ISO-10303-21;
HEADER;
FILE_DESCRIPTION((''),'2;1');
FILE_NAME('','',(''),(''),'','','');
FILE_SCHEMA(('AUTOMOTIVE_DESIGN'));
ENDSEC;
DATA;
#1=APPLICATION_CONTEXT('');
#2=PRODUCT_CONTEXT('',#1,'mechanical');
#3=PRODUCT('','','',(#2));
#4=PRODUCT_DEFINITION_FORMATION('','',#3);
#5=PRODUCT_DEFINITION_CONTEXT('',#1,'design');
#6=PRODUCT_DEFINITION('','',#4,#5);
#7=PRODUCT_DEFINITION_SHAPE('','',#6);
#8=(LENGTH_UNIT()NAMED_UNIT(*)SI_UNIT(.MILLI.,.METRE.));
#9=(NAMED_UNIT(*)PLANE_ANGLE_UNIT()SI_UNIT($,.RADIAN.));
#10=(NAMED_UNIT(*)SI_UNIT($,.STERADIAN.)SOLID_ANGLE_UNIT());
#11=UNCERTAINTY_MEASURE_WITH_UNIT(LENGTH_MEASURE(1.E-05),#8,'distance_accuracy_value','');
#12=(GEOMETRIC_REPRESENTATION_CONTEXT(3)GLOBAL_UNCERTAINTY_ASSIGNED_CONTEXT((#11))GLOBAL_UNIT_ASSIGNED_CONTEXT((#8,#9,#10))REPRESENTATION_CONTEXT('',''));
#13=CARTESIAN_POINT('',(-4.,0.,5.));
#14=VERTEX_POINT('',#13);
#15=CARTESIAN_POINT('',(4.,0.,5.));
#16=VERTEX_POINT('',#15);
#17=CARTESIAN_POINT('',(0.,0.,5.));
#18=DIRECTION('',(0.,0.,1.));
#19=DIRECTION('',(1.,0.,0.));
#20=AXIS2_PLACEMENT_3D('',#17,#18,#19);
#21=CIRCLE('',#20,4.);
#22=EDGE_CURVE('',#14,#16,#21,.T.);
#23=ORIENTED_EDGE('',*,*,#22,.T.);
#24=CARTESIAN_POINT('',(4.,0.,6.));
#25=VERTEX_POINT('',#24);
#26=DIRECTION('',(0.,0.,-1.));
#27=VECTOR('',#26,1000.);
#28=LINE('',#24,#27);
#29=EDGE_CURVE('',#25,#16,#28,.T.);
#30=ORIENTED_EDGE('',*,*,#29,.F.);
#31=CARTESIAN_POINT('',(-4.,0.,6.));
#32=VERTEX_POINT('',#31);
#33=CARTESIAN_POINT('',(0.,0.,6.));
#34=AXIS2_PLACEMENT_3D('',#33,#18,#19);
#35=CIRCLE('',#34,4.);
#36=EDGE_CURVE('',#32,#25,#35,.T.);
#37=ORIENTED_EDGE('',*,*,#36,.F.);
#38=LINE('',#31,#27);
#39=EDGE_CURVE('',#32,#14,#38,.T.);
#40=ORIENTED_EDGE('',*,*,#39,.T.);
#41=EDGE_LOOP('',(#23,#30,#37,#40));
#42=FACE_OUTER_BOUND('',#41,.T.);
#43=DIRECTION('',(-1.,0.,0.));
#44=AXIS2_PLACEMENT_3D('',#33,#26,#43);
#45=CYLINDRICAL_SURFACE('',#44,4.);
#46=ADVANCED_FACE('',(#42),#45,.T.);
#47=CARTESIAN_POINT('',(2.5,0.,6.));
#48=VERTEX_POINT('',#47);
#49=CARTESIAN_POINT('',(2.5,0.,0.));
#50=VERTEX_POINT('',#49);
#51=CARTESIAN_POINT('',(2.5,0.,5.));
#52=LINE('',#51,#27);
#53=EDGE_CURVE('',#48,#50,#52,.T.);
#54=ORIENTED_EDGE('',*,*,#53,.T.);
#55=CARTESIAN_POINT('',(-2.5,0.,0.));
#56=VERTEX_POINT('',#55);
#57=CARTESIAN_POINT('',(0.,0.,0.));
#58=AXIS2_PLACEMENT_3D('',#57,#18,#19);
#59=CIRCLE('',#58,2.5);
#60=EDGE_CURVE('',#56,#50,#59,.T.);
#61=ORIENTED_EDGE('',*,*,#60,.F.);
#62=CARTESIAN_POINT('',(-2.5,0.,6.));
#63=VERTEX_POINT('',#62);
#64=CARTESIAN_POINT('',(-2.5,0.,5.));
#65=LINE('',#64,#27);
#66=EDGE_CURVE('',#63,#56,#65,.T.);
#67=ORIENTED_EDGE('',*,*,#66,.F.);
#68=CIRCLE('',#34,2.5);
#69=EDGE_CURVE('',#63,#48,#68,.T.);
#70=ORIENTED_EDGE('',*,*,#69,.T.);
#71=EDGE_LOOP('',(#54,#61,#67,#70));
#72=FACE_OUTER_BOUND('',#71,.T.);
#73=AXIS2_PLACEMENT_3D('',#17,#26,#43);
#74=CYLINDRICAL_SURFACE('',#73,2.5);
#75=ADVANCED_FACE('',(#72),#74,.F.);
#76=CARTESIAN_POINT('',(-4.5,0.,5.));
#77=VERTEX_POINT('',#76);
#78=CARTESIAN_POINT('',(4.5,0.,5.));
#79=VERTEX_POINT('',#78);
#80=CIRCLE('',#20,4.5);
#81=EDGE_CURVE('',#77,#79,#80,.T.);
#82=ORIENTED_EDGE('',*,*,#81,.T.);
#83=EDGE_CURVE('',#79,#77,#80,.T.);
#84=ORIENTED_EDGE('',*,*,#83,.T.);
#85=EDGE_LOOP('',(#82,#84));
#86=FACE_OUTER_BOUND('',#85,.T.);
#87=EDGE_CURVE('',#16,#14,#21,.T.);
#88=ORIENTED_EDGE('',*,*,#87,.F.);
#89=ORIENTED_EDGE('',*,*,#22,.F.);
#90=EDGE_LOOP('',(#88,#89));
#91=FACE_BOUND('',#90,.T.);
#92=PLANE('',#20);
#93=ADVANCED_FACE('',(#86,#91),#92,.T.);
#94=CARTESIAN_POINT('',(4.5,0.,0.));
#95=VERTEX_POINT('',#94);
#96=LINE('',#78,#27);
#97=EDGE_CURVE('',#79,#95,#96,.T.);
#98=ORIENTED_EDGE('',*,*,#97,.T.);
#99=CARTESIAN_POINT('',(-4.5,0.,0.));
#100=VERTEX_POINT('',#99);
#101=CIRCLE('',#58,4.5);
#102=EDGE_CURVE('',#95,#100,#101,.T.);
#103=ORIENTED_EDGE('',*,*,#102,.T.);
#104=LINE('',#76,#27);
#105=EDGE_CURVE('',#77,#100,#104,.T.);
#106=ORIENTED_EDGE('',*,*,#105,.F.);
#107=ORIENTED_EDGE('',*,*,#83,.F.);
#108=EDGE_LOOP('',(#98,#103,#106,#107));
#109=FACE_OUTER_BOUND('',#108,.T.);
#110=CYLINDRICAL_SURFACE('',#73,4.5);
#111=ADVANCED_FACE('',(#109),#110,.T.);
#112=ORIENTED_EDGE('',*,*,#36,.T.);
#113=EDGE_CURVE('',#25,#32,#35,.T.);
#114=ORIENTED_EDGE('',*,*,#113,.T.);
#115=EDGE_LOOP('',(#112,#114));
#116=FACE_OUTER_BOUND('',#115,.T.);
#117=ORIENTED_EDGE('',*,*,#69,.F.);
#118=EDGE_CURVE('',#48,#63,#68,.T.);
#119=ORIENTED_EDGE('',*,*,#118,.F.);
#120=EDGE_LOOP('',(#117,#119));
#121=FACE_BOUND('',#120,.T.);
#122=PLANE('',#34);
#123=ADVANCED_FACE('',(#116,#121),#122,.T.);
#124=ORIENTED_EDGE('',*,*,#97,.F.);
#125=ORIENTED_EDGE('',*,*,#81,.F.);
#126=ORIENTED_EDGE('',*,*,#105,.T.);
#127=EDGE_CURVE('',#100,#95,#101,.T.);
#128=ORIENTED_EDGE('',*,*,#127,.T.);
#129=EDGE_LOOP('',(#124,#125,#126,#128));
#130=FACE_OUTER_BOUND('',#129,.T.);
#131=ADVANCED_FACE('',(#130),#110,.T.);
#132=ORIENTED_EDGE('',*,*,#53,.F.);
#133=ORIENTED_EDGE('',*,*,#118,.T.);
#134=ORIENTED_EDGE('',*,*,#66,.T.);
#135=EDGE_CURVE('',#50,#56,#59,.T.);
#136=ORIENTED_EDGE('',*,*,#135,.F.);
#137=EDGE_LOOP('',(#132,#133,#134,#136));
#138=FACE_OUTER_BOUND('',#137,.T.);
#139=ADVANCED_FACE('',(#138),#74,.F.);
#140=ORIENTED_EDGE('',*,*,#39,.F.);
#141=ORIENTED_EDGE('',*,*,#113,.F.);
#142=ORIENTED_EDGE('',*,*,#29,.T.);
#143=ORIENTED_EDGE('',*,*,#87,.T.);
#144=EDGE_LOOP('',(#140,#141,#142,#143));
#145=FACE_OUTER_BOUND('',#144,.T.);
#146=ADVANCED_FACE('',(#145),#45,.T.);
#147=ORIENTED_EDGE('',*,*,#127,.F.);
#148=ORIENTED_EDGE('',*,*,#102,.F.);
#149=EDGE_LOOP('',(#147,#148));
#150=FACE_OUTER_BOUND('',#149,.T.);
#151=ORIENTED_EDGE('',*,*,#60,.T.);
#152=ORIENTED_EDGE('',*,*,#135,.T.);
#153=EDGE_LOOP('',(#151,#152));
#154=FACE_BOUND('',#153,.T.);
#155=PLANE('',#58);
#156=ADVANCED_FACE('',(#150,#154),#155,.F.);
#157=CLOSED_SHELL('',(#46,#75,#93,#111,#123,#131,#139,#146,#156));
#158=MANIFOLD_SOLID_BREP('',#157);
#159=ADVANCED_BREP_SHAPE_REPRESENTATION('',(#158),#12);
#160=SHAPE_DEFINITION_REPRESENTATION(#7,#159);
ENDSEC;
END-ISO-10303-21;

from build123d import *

# Parameters (mm, degrees)
SKETCH_1_R      = 4.5
SKETCH_1_R_2    = 2.5
EXTRUDE_1_DEPTH = 5
SKETCH_2_R      = 4
SKETCH_2_R_2    = 2.5
EXTRUDE_2_DEPTH = 1


with BuildPart() as part:
    # 草图1 → 凸台-拉伸1 (new body)
    with BuildSketch(Plane.XY):
        Circle(SKETCH_1_R)
        Circle(SKETCH_1_R_2, mode=Mode.SUBTRACT)
    extrude(amount=EXTRUDE_1_DEPTH)

    # 草图2 → 凸台-拉伸2 (add)
    with BuildSketch(Plane.XY.offset(5)):
        Circle(SKETCH_2_R)
        Circle(SKETCH_2_R_2, mode=Mode.SUBTRACT)
    extrude(amount=EXTRUDE_2_DEPTH)


solid = part.part
